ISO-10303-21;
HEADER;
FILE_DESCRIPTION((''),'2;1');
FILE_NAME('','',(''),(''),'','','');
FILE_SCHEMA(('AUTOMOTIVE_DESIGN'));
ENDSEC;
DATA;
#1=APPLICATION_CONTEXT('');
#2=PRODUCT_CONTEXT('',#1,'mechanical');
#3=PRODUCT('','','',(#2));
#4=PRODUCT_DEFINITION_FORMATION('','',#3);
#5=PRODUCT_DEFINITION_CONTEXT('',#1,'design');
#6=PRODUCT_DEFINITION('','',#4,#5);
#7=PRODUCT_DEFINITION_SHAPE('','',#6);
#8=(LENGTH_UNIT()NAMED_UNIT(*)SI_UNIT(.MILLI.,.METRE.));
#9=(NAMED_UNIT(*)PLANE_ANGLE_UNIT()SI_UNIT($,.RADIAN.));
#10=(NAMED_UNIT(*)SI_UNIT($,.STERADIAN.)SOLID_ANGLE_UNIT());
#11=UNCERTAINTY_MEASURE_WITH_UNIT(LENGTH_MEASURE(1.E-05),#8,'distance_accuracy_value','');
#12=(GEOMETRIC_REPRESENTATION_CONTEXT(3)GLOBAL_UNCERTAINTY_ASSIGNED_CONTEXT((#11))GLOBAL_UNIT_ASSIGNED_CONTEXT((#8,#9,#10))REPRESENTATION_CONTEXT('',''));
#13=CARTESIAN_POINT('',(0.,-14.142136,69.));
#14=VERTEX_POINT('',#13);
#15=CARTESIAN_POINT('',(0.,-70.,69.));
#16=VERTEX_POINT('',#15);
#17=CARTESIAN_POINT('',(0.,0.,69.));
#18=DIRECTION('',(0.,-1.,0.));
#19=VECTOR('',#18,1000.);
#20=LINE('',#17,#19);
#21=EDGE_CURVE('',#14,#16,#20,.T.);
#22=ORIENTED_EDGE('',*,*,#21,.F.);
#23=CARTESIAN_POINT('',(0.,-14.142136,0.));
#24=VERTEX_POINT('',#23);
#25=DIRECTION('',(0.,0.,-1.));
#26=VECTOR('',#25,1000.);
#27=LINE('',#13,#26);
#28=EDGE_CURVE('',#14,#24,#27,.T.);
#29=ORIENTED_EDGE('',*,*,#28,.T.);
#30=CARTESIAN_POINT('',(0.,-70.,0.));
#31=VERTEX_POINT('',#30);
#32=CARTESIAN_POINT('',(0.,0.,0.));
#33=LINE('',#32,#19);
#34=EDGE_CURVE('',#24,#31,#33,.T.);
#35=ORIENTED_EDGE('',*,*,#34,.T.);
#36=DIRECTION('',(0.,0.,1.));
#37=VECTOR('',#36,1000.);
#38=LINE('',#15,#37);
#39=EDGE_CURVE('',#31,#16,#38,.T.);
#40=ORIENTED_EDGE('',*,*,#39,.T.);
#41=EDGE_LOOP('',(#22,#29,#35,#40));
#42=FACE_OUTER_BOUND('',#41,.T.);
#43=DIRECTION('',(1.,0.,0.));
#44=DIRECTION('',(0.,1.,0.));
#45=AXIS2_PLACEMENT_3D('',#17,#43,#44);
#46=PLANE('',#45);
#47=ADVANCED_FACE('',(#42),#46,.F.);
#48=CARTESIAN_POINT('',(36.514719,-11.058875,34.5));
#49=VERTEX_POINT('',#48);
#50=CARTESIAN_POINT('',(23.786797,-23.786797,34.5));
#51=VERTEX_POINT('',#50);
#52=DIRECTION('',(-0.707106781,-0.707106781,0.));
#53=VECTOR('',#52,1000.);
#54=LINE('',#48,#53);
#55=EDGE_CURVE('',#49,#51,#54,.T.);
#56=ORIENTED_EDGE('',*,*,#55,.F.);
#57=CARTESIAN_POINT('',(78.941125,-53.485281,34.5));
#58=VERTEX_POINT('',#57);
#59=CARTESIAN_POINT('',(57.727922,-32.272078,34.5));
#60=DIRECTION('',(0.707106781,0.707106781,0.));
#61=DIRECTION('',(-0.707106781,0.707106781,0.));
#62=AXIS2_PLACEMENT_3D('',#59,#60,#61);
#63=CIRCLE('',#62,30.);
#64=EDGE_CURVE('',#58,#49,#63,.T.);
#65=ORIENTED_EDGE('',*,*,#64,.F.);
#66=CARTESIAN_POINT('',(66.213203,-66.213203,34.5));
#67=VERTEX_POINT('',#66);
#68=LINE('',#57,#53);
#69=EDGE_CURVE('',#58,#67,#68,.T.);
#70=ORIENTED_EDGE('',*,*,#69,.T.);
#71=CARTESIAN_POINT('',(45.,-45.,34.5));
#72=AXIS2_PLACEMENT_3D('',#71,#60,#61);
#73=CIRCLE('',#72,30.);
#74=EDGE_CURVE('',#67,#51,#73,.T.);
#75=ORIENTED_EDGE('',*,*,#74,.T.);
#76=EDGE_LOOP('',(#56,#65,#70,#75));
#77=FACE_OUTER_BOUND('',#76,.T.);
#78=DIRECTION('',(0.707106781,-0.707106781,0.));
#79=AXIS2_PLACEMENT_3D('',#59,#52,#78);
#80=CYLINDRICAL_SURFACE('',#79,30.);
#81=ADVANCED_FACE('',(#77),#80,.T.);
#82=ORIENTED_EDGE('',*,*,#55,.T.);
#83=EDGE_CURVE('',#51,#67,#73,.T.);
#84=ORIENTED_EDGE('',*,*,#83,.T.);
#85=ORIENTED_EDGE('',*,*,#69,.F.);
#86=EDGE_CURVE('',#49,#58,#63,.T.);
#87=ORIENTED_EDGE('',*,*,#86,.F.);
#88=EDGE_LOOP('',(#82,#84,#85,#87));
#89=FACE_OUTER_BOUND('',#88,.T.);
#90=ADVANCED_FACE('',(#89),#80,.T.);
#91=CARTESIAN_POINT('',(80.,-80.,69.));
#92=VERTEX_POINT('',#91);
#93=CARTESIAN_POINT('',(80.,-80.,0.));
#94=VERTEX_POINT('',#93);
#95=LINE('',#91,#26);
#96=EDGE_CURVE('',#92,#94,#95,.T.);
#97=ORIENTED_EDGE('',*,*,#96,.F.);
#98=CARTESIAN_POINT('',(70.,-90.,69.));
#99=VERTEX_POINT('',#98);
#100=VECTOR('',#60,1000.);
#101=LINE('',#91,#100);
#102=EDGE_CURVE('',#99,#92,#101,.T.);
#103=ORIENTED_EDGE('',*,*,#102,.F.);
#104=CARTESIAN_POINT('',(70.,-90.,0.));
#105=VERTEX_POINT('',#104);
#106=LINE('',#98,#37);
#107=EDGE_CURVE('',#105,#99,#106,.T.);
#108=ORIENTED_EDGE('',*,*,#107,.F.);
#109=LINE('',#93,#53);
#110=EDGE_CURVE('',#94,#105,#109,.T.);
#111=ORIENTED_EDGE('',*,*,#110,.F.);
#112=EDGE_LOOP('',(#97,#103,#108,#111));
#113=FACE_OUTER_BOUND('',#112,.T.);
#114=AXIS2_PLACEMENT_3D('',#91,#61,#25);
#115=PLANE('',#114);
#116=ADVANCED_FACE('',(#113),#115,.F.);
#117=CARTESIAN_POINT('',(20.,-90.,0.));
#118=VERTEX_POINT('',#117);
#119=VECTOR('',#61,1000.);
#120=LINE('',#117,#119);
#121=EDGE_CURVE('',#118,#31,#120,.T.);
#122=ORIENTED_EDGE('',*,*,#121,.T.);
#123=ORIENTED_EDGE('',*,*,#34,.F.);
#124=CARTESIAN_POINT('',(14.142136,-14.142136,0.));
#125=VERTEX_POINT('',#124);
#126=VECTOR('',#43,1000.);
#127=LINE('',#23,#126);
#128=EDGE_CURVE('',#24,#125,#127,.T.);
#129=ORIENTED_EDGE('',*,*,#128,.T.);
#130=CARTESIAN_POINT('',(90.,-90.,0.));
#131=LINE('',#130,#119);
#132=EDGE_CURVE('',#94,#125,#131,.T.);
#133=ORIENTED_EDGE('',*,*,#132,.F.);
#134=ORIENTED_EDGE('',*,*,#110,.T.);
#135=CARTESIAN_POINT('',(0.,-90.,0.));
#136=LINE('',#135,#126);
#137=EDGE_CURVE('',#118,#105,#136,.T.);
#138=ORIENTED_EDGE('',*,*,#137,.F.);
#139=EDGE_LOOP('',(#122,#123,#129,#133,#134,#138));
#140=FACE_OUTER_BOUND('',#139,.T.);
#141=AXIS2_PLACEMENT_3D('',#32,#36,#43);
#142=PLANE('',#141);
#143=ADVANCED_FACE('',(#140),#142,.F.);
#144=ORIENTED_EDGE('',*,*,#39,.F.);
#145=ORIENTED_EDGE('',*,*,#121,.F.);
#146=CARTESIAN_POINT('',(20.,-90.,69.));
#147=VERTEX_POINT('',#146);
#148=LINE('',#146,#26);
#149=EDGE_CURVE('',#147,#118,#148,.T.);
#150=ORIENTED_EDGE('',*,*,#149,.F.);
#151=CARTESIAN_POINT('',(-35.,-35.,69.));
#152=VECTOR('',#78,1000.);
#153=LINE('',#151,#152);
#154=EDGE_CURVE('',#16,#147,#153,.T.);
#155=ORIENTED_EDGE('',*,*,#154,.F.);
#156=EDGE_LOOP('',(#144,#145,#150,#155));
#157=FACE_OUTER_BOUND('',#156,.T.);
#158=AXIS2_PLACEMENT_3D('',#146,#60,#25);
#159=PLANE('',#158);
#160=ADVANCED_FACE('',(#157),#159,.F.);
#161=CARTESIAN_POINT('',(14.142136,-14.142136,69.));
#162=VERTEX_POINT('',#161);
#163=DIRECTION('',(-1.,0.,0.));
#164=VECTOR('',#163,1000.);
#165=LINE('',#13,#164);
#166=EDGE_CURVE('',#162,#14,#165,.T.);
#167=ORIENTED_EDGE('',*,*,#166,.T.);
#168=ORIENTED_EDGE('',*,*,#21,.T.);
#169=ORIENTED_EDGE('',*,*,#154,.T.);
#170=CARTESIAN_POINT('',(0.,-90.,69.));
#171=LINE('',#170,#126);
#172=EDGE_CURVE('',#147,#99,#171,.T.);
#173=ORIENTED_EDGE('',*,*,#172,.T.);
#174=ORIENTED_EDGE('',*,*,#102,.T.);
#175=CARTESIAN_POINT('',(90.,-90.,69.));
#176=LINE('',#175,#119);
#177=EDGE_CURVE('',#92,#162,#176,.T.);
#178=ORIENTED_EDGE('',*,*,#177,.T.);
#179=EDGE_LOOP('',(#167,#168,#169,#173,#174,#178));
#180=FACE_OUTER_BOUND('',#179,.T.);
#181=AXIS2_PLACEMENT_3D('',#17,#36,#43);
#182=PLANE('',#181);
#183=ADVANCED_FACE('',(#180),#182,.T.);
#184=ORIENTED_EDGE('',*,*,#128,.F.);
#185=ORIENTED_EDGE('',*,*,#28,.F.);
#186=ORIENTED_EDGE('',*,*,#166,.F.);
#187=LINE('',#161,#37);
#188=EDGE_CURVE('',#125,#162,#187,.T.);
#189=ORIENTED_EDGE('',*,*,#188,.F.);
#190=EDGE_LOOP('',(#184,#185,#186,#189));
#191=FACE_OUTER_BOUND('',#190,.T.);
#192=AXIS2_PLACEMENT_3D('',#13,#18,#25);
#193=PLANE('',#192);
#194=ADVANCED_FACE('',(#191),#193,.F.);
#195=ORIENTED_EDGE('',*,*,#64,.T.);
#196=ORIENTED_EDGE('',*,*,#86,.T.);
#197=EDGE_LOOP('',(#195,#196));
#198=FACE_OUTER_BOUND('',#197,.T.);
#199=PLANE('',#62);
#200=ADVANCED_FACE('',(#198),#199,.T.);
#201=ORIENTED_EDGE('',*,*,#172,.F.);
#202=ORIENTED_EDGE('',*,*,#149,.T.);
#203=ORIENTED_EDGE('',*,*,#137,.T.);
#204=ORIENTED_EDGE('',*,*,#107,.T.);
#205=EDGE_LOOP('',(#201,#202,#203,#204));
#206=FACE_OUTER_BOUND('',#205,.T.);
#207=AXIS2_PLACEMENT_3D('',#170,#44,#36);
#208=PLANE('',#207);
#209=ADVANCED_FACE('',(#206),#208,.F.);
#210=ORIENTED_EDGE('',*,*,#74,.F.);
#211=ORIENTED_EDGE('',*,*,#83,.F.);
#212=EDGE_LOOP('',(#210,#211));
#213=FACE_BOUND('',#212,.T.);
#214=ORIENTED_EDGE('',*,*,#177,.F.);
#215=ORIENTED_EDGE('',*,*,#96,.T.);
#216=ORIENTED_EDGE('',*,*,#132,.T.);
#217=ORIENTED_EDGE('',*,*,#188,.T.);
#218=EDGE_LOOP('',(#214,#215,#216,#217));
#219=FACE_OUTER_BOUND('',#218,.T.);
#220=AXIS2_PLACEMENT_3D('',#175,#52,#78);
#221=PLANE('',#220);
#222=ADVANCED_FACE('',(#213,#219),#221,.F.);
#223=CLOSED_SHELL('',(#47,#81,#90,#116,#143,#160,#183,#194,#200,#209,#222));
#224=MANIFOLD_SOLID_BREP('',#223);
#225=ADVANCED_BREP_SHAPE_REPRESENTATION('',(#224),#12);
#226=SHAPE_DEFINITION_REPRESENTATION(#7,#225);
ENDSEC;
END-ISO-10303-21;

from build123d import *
from OCP.BRepFilletAPI import BRepFilletAPI_MakeChamfer

# Parameters (mm, degrees)
EXTRUDE_1_DEPTH = 69
CHAMFER_1_SIZE  = 20
SKETCH_3_R      = 30
EXTRUDE_2_DEPTH = 18
CHAMFER_2_SIZE  = 20
CHAMFER_2_SIZE2 = 14.142135624


with BuildPart() as part:
    # 草图1 → 凸台-拉伸1 (new body)
    with BuildSketch(Plane.XY):
        Polygon((0, 0), (0, -90), (90, -90), align=None)
    extrude(amount=EXTRUDE_1_DEPTH)

    # 倒角1
    chamfer_1_edges = [part.edges().sort_by_distance(p)[0] for p in [
        (0, -90, 34.5),
    ]]
    chamfer(chamfer_1_edges, length=CHAMFER_1_SIZE)

    # 草图3 → 凸台-拉伸2 (add)
    with BuildSketch(Plane(origin=(0, 0, 0), x_dir=(0, 0, -1), z_dir=(0.7071067811865475, 0.7071067811865476, 0))):
        with Locations(Location((-34.5, -63.639610307, 0), (0, 0, 90))):
            Circle(SKETCH_3_R)
    extrude(amount=EXTRUDE_2_DEPTH)

    # 倒角2: one chamfer whose edges measure the first distance from different faces: ONE call of the kernel's chamfer builder (chamfer() names one face for all edges)
    chamfer_2_edges_1 = [part.edges().sort_by_distance(p)[0] for p in [
        (90, -90, 34.5),
    ]]
    chamfer_2_side_1 = [part.faces().sort_by_distance(p)[0] for p in [
        (55, -90, 34.5),
    ]]
    chamfer_2_edges_2 = [part.edges().sort_by_distance(p)[0] for p in [
        (0, 0, 34.5),
    ]]
    chamfer_2_side_2 = [part.faces().sort_by_distance(p)[0] for p in [
        (88.976256868, -88.976256868, 34.5),
    ]]
    chamfer_2 = BRepFilletAPI_MakeChamfer(part.part.solid().wrapped)
    for e in chamfer_2_edges_1:
        chamfer_2.Add(CHAMFER_2_SIZE, CHAMFER_2_SIZE2, e.wrapped, chamfer_2_side_1[0].wrapped)  # the first distance lies on this face
    for e in chamfer_2_edges_2:
        chamfer_2.Add(CHAMFER_2_SIZE, CHAMFER_2_SIZE2, e.wrapped, chamfer_2_side_2[0].wrapped)  # the first distance lies on this face
    add(Compound.cast(chamfer_2.Shape()), mode=Mode.REPLACE)


solid = part.part
